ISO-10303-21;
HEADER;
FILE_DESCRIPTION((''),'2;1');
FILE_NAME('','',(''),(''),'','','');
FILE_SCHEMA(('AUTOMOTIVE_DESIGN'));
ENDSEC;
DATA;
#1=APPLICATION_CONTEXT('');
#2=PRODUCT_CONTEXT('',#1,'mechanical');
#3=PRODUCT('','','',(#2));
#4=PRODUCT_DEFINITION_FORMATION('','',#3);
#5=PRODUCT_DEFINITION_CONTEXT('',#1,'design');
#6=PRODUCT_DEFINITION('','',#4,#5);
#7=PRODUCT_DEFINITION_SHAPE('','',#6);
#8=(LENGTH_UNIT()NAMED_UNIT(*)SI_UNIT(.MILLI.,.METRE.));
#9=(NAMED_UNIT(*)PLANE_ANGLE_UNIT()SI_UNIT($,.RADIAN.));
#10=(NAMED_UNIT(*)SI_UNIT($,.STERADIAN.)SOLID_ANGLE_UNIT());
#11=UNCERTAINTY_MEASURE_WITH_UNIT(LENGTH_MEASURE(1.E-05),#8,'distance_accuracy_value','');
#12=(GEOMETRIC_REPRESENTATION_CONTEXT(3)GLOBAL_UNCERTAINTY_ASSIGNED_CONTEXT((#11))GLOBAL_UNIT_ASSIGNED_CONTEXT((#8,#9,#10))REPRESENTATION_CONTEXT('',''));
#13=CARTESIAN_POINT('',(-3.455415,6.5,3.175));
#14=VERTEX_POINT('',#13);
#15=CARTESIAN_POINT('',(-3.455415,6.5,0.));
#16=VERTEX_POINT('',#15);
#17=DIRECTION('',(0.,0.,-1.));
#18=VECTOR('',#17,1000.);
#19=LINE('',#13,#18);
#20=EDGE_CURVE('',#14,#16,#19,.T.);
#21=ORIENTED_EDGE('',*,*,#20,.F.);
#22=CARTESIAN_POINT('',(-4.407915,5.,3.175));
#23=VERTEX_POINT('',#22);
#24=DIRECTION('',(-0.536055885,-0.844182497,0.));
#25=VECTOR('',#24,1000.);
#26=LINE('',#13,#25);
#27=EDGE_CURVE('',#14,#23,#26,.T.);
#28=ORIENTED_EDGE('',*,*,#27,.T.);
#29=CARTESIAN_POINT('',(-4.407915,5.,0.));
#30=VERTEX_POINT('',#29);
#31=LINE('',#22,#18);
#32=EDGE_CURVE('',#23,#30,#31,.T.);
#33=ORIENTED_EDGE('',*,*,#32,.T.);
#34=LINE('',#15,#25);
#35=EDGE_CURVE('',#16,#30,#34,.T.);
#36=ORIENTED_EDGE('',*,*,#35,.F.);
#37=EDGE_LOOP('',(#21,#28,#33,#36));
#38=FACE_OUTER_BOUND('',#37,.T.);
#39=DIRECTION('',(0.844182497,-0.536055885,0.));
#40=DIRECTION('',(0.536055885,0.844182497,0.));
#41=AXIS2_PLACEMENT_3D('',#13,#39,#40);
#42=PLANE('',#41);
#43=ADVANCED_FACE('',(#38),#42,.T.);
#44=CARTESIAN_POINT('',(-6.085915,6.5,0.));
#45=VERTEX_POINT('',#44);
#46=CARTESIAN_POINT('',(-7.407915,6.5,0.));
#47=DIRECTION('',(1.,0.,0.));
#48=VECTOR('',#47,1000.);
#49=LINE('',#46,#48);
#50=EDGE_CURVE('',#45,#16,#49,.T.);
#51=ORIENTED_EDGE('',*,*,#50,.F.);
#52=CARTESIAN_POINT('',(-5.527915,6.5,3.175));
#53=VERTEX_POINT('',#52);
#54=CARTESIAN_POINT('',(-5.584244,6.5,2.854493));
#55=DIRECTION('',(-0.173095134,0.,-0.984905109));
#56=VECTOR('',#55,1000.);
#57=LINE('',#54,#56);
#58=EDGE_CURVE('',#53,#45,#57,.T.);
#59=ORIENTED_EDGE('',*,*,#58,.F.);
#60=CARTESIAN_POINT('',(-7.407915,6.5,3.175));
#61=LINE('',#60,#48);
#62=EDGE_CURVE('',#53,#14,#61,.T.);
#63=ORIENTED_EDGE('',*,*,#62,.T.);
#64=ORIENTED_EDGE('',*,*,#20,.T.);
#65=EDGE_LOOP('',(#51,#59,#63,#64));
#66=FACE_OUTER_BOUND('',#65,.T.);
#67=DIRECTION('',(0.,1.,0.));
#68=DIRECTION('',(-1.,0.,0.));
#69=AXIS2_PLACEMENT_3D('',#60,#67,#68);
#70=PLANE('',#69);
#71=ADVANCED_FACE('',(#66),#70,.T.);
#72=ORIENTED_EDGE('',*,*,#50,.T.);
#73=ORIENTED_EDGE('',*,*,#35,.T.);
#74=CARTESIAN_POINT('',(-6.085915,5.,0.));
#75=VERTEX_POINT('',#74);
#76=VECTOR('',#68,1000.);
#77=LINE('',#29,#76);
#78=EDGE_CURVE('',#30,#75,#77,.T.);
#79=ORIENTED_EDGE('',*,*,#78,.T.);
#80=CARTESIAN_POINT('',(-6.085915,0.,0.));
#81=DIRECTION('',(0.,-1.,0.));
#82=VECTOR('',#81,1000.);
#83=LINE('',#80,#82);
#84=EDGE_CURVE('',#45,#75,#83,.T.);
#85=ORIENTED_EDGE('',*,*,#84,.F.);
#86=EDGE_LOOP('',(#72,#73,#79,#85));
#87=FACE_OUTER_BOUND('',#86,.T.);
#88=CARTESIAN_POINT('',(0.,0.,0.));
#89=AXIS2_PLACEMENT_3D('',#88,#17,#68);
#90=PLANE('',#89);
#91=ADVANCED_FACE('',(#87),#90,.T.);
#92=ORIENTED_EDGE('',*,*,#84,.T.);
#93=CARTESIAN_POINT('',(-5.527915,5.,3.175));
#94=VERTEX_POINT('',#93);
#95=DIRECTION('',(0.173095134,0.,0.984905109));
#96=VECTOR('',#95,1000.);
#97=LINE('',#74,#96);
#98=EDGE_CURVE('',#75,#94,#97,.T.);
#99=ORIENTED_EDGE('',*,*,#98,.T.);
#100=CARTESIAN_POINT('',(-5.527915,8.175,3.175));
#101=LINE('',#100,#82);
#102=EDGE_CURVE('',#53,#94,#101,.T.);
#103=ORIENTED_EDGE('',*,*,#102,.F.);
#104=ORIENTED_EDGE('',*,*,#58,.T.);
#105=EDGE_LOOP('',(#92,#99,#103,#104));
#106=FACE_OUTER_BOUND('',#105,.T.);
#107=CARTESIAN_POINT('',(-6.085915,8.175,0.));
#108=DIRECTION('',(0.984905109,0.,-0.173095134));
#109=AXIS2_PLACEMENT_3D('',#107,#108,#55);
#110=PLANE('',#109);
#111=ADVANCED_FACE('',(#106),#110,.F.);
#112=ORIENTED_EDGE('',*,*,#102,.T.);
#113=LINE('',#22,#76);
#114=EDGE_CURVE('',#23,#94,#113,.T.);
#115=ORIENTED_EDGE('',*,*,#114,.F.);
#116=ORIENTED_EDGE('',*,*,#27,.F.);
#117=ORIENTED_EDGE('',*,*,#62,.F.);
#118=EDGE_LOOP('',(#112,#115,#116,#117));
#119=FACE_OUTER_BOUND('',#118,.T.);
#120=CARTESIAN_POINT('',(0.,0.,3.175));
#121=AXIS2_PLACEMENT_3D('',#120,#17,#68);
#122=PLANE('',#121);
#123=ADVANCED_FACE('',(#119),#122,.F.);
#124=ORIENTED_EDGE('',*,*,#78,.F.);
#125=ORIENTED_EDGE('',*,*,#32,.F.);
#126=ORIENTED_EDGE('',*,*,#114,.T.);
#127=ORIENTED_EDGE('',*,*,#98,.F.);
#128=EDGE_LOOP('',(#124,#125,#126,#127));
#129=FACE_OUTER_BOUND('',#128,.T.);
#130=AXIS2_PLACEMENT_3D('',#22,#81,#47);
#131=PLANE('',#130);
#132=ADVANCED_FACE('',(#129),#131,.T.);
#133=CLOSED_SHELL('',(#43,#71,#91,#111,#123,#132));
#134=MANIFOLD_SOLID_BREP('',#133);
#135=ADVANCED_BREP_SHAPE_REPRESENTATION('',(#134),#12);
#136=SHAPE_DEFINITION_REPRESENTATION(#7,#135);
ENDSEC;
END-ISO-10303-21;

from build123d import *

# Parameters (mm, degrees)
EXTRUDE_1_DEPTH     = 3.175
CUT_EXTRUDE_1_DEPTH = 3.175


with BuildPart() as part:
    # 草图1 → 凸台-拉伸1 (new body)
    with BuildSketch(Plane.XY):
        Polygon((-4.407915319, 5), (-7.407915319, 5), (-7.407915319, 6.5), (-3.455415319, 6.5), align=None)
    extrude(amount=EXTRUDE_1_DEPTH)

    # 草图3 → 切除-拉伸1 (cut)
    with BuildSketch(Plane.XZ.offset(-5)):
        Polygon((-7.407915319, 0), (-6.085915319, 0), (-5.527915319, 3.175), (-7.407915319, 3.175), align=None)
    extrude(amount=-CUT_EXTRUDE_1_DEPTH, mode=Mode.SUBTRACT)


solid = part.part
